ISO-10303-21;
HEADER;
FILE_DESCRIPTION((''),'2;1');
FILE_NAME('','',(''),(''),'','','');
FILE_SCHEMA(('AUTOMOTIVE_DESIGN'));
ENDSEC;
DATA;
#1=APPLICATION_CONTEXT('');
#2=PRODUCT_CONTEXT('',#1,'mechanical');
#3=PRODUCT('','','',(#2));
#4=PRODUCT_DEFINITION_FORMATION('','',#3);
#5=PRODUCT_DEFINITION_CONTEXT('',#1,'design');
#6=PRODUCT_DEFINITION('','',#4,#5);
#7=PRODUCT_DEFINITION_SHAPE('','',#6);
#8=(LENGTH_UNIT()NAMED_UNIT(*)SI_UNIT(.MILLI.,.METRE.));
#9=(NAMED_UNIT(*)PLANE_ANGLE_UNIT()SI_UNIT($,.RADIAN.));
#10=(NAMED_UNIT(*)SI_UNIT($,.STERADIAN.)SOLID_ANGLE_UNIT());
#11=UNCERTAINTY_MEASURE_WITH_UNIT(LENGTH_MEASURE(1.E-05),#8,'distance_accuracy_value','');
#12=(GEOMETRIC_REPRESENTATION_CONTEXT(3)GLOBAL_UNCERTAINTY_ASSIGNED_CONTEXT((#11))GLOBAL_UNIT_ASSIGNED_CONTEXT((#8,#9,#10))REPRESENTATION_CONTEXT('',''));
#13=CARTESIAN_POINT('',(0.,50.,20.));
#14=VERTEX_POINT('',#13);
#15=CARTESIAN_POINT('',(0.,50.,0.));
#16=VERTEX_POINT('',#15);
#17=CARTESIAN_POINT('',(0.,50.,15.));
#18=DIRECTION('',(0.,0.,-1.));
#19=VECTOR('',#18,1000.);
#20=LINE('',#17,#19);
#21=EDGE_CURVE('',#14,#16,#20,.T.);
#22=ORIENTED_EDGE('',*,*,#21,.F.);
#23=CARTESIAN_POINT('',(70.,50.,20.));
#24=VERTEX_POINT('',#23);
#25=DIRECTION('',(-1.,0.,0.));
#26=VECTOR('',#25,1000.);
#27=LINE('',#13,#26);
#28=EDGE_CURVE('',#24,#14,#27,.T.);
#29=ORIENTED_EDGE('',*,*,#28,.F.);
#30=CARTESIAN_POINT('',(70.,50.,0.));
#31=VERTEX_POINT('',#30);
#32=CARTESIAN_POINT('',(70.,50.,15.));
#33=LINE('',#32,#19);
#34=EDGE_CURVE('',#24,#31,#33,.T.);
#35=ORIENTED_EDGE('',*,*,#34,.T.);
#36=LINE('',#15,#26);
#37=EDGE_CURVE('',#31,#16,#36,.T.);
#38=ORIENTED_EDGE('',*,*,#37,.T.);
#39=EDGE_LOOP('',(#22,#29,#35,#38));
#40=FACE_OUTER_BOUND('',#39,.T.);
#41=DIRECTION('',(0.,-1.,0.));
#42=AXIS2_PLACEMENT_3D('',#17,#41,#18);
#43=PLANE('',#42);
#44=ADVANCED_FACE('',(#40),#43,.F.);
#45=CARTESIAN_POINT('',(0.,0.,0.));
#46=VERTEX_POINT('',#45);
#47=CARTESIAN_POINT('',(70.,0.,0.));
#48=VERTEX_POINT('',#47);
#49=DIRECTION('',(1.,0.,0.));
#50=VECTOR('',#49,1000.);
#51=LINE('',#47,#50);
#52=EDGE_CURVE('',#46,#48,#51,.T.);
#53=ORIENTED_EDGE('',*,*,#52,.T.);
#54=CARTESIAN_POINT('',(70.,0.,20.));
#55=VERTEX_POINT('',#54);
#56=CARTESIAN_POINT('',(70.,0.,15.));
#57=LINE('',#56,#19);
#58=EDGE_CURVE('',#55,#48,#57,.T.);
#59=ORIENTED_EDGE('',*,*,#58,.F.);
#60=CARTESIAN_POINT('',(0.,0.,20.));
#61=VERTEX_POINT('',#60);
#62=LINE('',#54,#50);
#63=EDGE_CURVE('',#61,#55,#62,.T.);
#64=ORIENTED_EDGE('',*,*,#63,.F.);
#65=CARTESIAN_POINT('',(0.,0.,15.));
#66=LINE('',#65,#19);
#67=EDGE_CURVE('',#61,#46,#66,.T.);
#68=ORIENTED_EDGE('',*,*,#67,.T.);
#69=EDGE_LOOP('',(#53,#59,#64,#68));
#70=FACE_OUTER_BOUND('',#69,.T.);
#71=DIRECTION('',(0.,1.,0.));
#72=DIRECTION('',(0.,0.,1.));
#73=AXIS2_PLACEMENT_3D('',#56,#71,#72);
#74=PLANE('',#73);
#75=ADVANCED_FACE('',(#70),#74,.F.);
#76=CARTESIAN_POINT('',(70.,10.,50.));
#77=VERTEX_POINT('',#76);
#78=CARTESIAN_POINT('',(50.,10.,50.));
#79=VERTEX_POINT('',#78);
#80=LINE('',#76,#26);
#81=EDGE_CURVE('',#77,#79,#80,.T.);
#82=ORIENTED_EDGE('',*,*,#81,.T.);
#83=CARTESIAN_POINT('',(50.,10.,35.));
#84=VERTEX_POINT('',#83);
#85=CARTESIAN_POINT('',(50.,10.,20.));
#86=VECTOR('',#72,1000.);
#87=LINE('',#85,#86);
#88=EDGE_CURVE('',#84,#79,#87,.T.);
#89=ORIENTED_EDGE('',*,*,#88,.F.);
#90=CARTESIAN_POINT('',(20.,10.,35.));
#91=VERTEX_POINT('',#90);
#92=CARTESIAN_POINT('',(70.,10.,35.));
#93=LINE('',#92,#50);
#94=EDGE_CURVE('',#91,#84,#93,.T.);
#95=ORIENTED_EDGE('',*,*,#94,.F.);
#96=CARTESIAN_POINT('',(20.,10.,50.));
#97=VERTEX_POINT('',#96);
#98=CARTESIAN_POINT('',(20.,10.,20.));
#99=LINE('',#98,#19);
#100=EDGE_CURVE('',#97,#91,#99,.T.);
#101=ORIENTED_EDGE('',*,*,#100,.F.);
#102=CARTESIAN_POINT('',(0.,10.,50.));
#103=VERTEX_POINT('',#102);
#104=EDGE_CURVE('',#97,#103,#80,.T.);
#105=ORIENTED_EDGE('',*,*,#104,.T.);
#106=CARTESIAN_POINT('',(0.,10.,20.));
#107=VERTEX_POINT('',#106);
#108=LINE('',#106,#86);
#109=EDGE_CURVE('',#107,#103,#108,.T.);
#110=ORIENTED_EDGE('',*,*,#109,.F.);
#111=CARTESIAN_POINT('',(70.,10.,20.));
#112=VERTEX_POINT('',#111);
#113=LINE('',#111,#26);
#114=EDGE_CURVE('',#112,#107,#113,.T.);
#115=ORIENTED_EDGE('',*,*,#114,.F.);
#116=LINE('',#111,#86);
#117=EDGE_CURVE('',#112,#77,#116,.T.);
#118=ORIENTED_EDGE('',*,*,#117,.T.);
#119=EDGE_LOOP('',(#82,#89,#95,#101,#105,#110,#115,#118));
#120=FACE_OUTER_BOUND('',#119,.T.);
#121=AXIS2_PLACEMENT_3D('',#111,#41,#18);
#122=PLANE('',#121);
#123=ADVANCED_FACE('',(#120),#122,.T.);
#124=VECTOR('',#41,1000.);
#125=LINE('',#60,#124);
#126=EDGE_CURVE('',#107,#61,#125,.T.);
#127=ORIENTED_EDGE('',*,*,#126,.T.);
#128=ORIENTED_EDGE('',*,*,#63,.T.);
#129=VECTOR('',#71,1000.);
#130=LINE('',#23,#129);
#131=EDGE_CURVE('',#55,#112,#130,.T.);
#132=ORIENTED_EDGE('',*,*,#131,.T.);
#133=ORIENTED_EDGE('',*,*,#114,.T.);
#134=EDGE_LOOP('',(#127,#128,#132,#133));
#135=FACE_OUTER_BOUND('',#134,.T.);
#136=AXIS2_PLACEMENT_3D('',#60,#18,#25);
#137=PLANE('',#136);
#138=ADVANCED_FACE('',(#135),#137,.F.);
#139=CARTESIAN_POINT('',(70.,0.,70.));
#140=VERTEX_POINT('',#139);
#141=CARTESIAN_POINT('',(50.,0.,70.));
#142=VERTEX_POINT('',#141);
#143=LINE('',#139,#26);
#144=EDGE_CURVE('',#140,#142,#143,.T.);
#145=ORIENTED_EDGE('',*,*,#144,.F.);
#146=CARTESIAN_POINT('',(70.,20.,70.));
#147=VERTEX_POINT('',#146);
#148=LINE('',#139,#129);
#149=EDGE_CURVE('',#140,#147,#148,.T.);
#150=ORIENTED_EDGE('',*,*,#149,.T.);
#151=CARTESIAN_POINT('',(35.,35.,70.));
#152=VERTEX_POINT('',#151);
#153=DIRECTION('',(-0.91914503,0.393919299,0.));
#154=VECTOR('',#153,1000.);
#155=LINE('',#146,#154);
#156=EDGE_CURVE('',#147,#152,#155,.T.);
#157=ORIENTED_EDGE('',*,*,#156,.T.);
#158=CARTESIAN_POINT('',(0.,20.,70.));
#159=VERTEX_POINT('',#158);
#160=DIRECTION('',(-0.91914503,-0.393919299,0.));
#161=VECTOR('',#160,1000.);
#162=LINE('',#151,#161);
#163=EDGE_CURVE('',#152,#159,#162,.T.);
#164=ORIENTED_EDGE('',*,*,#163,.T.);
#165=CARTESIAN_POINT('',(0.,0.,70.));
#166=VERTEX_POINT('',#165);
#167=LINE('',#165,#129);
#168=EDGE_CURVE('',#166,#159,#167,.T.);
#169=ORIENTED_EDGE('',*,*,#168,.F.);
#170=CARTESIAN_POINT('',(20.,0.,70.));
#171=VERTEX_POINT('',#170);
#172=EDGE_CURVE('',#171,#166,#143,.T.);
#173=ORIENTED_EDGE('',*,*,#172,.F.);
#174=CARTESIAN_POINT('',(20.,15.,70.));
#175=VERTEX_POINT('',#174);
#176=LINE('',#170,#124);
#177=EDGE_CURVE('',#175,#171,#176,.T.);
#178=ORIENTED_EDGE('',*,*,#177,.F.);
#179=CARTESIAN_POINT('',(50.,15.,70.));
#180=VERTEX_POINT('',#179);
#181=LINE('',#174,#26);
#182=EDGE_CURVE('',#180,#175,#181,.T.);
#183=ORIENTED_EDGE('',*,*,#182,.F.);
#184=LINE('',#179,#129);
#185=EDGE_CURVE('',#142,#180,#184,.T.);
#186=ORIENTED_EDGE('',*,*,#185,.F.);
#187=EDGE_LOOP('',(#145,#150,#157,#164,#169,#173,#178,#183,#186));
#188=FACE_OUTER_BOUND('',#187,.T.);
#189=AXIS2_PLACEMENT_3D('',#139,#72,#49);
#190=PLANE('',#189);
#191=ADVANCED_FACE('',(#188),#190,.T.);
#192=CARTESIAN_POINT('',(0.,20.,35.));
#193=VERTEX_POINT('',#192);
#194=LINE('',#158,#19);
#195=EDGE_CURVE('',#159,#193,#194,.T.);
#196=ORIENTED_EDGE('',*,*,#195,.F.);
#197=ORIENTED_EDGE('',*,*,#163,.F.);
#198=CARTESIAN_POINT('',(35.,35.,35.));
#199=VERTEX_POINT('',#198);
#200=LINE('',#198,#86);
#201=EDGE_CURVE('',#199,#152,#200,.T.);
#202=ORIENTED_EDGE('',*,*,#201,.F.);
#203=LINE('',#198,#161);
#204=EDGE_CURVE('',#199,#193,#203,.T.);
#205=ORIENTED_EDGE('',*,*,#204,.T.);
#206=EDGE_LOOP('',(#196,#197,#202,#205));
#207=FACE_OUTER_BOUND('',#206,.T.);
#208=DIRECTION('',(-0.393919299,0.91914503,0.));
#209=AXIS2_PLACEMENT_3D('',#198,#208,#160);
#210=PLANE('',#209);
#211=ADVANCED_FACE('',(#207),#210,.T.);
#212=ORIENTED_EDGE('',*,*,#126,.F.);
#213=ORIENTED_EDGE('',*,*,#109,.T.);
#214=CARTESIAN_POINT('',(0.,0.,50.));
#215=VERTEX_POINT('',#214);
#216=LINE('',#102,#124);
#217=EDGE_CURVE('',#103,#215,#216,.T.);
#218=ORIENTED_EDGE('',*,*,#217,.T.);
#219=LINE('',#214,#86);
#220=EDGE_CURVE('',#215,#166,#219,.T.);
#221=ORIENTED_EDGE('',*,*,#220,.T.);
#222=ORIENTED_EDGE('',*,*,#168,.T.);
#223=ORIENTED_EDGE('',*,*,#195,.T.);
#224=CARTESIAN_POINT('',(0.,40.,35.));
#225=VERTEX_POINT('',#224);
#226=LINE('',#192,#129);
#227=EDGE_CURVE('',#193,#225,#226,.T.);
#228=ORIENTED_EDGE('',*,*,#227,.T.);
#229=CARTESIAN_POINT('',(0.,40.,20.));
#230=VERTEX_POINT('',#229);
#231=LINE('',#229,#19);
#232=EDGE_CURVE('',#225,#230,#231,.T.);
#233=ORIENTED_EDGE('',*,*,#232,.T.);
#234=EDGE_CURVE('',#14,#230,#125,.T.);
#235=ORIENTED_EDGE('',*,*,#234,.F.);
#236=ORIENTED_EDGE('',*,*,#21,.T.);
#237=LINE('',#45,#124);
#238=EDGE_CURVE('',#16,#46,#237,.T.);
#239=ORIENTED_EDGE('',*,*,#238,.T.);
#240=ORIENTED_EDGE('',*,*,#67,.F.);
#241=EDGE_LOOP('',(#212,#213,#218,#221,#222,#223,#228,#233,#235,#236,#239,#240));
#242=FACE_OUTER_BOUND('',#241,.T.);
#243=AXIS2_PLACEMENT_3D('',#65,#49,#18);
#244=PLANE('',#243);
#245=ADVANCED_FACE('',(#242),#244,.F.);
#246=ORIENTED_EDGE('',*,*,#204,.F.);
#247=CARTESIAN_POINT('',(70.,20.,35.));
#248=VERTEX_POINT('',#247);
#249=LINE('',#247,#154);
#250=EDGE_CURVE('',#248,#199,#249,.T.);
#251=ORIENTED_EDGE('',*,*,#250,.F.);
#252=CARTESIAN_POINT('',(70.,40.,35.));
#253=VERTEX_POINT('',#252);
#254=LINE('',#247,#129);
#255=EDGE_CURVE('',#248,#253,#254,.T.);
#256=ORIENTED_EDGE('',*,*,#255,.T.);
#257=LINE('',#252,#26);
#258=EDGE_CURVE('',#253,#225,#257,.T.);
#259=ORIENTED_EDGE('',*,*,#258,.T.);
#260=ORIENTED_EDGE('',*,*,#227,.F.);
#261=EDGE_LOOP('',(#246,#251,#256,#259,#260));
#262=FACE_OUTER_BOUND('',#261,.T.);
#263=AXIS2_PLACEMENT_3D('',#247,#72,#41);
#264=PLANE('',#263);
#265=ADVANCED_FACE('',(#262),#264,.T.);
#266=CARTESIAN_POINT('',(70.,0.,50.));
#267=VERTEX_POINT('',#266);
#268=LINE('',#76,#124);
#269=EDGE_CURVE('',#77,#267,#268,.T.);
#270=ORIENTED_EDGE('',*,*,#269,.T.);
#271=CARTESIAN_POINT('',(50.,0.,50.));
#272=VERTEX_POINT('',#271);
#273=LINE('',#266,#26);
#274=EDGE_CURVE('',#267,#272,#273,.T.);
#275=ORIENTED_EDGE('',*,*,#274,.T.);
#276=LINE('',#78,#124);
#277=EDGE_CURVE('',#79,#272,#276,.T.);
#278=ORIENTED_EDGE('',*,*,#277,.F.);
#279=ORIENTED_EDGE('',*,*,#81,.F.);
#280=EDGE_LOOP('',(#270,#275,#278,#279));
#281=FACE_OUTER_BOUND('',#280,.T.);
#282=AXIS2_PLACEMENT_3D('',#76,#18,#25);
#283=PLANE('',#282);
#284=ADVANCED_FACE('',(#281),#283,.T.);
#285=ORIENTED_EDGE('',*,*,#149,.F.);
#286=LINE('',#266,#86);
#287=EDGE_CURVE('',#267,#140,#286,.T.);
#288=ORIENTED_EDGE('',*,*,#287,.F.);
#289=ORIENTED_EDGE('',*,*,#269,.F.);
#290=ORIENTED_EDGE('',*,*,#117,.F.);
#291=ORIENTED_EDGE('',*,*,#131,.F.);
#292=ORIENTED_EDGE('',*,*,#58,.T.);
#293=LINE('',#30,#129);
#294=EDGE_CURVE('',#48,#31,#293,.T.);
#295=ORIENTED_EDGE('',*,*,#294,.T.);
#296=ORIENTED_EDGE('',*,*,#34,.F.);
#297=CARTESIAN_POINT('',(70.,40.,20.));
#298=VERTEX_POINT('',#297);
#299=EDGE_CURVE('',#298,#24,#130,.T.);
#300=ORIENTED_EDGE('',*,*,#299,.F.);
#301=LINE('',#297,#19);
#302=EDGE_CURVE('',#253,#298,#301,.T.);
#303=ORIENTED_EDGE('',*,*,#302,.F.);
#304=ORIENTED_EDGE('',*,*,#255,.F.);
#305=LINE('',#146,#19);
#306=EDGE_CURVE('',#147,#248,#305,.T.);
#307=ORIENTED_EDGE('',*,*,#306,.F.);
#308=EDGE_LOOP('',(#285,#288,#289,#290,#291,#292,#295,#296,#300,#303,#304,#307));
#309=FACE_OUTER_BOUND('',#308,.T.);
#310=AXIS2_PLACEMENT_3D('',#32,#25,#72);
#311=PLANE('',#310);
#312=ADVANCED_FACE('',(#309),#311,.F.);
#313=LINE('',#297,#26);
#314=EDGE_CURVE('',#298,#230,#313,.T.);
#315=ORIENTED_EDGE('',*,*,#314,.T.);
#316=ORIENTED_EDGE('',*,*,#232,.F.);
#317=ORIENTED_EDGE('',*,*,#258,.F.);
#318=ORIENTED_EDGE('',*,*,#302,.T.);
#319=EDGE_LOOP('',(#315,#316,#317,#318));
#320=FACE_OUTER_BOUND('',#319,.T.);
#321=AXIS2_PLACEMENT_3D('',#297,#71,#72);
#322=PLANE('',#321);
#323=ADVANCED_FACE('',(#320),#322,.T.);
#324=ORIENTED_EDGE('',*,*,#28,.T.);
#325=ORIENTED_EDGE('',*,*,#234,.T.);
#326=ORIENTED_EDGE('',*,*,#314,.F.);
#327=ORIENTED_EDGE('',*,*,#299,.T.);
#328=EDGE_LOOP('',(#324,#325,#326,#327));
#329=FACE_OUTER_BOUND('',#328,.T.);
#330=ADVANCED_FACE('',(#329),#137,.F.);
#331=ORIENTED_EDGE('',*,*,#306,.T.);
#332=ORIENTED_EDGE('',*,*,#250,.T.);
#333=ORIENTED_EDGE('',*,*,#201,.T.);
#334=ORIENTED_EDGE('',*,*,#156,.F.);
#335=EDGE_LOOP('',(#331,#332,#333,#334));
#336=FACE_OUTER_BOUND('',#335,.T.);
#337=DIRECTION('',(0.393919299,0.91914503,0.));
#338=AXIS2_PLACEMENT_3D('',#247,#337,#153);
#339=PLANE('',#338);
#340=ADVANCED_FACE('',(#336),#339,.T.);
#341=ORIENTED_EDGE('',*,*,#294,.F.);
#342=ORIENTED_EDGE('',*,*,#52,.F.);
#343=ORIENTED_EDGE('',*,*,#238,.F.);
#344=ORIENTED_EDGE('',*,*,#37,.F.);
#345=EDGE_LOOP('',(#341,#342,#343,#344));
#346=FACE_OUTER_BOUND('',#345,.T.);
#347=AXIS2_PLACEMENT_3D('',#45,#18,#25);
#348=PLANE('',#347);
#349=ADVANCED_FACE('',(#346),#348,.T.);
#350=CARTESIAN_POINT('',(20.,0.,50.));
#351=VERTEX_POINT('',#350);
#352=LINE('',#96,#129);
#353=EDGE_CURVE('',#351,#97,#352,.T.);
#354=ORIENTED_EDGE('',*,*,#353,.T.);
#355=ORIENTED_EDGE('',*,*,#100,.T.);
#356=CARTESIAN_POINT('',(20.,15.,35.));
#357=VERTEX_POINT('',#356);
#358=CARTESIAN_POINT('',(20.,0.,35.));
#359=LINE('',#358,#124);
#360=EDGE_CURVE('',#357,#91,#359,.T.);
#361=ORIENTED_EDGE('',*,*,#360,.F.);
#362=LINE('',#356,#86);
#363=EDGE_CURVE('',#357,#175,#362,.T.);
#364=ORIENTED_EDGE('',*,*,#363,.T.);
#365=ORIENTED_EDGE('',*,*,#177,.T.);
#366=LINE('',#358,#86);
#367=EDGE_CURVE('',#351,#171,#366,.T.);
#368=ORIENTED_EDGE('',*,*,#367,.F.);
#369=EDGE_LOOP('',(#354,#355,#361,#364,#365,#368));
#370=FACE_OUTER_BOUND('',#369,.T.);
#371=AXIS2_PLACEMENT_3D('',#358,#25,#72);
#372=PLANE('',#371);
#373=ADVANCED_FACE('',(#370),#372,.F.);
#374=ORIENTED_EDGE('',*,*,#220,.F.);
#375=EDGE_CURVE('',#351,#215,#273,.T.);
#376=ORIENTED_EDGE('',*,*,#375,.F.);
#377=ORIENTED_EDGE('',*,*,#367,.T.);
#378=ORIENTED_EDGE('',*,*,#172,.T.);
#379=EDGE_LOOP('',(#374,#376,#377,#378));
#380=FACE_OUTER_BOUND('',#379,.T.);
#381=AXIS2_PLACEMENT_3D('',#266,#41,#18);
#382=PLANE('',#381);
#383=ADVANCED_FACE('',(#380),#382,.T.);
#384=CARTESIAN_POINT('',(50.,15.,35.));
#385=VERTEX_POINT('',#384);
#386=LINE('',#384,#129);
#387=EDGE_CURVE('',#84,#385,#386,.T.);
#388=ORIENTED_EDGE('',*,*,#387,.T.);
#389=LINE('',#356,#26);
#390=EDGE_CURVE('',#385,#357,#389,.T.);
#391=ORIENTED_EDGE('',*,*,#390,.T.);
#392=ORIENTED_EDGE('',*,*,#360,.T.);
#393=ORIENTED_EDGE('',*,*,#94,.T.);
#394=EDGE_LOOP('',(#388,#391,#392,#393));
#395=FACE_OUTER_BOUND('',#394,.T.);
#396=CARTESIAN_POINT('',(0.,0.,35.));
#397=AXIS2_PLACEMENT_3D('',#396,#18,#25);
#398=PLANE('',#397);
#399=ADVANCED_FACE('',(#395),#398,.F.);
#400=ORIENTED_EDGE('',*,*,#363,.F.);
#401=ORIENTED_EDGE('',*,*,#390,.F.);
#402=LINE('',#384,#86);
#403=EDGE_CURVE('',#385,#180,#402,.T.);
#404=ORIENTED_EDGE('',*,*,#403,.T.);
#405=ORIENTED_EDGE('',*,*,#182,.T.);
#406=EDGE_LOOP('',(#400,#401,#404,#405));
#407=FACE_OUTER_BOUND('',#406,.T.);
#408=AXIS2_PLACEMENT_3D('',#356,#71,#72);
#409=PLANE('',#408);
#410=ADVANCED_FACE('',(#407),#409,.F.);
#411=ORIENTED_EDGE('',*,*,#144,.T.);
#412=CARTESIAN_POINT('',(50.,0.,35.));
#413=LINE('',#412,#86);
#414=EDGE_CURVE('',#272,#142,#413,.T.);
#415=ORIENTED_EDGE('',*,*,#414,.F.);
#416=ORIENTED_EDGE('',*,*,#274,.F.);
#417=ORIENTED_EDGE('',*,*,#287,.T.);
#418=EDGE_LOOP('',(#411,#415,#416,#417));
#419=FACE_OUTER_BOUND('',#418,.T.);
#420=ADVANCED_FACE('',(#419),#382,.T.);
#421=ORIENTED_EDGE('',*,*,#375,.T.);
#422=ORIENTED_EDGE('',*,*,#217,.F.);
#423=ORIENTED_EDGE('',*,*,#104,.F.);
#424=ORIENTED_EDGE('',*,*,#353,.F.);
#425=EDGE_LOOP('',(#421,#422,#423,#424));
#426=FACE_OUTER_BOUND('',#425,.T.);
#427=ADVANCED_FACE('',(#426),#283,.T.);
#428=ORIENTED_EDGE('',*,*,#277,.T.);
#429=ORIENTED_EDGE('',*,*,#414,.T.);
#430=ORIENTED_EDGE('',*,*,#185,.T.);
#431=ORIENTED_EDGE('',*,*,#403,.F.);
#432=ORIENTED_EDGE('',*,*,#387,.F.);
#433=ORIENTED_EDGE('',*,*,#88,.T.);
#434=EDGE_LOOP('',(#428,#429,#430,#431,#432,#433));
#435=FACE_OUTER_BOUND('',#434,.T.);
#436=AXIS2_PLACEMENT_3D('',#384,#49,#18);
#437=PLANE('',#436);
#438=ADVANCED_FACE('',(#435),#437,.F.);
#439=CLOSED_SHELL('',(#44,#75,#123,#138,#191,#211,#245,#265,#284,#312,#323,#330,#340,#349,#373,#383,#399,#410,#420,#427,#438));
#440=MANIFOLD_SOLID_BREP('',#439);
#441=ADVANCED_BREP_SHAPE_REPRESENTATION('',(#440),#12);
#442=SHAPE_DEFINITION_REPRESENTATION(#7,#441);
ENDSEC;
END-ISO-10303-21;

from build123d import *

# Parameters (mm, degrees)
BASE_BLOCK_SKETCH_W  = 70
BASE_BLOCK_SKETCH_H  = 50
BASE_BLOCK_DEPTH     = 15
PAD_SKETCH_W         = 70
PAD_SKETCH_H         = 50
PAD_5MM_DEPTH        = 5
STEPPED_BODY_DEPTH   = 70
ANGLED_WEDGE_DEPTH   = 35
FRONT_SLOT_CUT_DEPTH = 35


with BuildPart() as part:
    # Base Block Sketch → Base Block (new body)
    with BuildSketch(Plane.XY):
        with Locations((35, 25)):
            Rectangle(BASE_BLOCK_SKETCH_W, BASE_BLOCK_SKETCH_H)
    extrude(amount=BASE_BLOCK_DEPTH)

    # Pad Sketch → Pad 5mm (add)
    with BuildSketch(Plane.XY.offset(15)):
        with Locations((35, 25)):
            Rectangle(PAD_SKETCH_W, PAD_SKETCH_H)
    extrude(amount=PAD_5MM_DEPTH)

    # Stepped Profile Sketch → Stepped Body (add)
    with BuildSketch(Plane.ZY):
        Polygon((20, 40), (35, 40), (35, 20), (70, 20), (70, 0), (50, 0), (50, 10), (20, 10), align=None)
    extrude(amount=-STEPPED_BODY_DEPTH)

    # Wedge Sketch → Angled Wedge (add)
    with BuildSketch(Plane.XY.offset(70)):
        Polygon((35, 35), (0, 20), (70, 20), align=None)
    extrude(amount=-ANGLED_WEDGE_DEPTH)

    # Slot Cut Sketch → Front Slot Cut (cut)
    with BuildSketch(Plane.XY.offset(70)):
        Polygon((35, 0), (20, 0), (20, 15), (50, 15), (50, 0), align=None)
    extrude(amount=-FRONT_SLOT_CUT_DEPTH, mode=Mode.SUBTRACT)


solid = part.part
